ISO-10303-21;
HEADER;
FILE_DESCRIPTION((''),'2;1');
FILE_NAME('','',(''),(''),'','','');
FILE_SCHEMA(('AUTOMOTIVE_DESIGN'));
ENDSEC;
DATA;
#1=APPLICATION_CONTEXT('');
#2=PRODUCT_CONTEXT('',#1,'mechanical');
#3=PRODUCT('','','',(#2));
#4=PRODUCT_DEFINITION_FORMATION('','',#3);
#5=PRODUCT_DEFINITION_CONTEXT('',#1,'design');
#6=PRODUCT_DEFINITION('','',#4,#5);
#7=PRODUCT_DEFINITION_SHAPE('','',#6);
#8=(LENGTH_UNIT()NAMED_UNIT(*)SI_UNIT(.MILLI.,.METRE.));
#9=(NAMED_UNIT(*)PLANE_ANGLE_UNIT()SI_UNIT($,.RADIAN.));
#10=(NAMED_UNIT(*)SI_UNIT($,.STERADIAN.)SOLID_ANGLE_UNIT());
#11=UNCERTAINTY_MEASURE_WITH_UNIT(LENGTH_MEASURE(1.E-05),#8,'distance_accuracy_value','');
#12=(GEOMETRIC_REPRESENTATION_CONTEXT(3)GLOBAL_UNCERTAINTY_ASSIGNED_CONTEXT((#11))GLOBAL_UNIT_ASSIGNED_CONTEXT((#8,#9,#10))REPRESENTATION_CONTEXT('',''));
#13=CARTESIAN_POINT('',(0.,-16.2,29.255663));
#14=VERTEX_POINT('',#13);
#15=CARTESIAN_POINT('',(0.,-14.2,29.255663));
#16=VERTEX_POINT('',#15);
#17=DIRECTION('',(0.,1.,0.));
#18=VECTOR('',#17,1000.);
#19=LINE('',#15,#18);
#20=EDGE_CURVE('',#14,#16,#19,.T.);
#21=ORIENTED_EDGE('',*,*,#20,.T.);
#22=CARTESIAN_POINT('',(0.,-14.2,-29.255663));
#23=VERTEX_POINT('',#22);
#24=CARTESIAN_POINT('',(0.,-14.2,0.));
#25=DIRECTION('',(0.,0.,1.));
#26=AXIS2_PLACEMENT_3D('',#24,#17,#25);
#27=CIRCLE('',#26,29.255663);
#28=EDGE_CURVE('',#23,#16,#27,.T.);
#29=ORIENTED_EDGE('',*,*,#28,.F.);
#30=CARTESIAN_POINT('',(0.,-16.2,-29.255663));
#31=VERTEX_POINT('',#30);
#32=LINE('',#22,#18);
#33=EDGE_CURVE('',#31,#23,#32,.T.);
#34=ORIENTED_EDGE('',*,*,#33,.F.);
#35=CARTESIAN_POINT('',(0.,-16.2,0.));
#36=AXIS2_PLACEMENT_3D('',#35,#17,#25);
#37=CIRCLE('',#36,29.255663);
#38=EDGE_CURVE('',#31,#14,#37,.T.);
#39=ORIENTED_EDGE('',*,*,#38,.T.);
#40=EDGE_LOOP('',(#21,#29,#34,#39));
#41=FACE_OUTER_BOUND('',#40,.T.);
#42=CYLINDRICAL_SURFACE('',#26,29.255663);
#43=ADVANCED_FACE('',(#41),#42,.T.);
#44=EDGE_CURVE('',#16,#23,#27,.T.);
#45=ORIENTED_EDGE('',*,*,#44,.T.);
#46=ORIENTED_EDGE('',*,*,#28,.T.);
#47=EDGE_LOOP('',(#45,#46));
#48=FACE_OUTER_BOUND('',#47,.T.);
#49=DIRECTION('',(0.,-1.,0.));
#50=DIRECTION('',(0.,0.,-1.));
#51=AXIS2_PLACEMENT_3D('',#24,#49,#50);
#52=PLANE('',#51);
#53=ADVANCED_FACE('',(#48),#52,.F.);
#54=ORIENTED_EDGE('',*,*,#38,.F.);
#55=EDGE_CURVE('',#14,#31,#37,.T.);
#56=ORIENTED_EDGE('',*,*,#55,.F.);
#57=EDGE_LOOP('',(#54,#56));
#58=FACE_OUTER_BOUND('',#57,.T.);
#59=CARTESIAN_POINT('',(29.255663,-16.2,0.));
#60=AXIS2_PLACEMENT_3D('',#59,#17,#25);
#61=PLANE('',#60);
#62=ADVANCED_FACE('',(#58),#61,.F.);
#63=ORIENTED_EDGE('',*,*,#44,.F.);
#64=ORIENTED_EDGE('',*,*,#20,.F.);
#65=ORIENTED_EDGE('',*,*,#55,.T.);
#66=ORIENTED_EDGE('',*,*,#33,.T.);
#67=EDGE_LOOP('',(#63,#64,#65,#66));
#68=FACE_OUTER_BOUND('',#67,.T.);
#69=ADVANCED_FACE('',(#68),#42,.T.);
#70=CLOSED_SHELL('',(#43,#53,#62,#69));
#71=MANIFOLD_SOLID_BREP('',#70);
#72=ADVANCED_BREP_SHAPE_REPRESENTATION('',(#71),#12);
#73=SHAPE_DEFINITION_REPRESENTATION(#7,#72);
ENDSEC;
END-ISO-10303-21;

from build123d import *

# Parameters (mm, degrees)
SKETCH_1_W = 29.255663301
SKETCH_1_H = 2


with BuildPart() as part:
    # 草图1 → 旋转1 (revolve)
    with BuildSketch(Plane.XY, mode=Mode.PRIVATE) as revolve_1_sk:
        with Locations((14.627831651, -15.2)):
            Rectangle(SKETCH_1_W, SKETCH_1_H)
    revolve(revolve_1_sk.sketch.rotate(Axis((0, -14.2, 0), (0, 1, 0)), 270), axis=Axis((0, -14.2, 0), (0, 1, 0)))


solid = part.part
